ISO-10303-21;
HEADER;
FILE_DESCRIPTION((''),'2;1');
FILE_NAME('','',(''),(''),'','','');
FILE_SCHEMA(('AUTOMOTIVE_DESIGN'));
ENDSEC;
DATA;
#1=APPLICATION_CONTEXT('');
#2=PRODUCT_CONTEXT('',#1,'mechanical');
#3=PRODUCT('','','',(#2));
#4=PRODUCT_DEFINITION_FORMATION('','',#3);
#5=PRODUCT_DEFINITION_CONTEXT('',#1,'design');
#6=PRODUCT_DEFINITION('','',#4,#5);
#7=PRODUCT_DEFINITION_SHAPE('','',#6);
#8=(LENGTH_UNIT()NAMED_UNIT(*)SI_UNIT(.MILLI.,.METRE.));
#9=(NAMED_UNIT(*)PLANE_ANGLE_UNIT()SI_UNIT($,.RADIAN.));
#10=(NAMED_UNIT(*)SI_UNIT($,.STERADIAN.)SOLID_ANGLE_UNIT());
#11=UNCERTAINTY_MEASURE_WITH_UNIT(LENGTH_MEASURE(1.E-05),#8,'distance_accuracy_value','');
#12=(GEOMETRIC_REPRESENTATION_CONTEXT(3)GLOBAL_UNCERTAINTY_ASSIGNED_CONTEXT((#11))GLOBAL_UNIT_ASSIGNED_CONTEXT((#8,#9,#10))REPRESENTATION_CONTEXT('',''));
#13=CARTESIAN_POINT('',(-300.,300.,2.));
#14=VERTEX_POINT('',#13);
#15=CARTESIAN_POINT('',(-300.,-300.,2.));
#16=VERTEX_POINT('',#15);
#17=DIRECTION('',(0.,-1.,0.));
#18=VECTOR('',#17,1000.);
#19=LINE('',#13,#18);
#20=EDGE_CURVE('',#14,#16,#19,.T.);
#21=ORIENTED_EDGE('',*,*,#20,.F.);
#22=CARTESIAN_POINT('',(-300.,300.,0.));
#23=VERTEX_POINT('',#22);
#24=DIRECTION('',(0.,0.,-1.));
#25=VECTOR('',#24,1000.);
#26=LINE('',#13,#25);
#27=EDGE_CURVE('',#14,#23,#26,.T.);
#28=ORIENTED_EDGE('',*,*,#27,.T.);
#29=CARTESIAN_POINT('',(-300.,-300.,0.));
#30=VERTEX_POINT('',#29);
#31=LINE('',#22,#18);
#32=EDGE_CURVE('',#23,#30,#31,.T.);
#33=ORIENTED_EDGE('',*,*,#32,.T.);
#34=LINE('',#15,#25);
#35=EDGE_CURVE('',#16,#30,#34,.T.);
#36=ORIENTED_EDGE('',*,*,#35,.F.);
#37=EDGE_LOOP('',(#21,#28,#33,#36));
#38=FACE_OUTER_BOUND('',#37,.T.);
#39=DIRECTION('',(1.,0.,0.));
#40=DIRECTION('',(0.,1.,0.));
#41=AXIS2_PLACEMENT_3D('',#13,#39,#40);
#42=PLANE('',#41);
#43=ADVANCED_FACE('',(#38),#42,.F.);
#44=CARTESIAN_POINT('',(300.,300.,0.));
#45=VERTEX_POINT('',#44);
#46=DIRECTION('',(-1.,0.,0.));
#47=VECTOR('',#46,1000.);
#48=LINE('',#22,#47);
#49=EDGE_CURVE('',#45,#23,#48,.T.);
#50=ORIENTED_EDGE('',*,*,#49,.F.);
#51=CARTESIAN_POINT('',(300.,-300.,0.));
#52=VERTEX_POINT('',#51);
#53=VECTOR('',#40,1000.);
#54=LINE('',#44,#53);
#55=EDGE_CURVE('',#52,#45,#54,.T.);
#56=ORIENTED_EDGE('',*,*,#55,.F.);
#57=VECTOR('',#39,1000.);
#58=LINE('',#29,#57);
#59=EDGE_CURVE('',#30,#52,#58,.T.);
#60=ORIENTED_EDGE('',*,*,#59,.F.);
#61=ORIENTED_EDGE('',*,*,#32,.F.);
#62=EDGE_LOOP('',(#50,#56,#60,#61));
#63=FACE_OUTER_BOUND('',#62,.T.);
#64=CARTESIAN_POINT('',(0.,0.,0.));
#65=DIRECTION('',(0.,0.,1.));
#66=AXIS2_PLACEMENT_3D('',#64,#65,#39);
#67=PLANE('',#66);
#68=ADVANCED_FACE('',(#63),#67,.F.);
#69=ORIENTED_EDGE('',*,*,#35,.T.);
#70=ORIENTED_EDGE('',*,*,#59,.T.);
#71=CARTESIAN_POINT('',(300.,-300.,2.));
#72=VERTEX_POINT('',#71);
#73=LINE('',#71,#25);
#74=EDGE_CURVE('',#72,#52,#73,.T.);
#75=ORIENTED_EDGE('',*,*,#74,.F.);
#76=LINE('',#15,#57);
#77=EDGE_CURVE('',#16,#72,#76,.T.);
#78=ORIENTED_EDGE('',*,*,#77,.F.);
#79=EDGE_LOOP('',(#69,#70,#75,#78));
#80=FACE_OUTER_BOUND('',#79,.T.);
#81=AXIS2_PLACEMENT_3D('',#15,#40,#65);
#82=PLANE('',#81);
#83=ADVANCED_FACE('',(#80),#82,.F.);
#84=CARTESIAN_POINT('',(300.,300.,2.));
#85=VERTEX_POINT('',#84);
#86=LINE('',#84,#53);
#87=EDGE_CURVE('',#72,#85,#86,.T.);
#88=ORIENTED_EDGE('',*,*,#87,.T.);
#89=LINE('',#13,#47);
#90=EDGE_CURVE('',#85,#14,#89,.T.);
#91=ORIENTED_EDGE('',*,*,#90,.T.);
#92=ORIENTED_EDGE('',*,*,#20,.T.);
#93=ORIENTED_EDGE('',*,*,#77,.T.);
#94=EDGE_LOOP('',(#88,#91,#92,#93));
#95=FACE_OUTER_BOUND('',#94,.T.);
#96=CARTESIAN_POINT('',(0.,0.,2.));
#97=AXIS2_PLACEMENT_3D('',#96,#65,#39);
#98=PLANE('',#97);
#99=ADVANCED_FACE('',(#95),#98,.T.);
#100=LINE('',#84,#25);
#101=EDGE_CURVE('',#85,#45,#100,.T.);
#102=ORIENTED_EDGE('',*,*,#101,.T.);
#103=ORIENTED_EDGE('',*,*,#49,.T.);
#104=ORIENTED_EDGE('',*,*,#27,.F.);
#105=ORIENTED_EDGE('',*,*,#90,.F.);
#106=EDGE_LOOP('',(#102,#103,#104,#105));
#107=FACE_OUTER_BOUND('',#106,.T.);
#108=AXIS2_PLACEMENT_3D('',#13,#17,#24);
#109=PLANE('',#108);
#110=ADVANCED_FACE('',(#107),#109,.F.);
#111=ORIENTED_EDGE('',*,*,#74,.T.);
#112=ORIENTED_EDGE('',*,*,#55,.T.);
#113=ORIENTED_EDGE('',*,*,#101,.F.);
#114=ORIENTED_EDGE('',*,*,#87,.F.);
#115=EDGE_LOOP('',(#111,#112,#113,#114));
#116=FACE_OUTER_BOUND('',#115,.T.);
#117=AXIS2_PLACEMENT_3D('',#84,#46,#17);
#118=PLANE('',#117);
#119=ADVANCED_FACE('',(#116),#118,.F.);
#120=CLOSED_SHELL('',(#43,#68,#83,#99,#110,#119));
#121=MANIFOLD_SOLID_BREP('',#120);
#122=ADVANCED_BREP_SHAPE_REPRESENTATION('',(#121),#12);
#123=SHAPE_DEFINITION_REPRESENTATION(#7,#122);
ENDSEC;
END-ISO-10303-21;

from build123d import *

# Parameters (mm, degrees)
SKETCH_1_W      = 600
SKETCH_1_H      = 600
EXTRUDE_1_DEPTH = 2


with BuildPart() as part:
    # 草图1 → 凸台-拉伸1 (new body)
    with BuildSketch(Plane.XY):
        Rectangle(SKETCH_1_W, SKETCH_1_H)
    extrude(amount=EXTRUDE_1_DEPTH)


solid = part.part
